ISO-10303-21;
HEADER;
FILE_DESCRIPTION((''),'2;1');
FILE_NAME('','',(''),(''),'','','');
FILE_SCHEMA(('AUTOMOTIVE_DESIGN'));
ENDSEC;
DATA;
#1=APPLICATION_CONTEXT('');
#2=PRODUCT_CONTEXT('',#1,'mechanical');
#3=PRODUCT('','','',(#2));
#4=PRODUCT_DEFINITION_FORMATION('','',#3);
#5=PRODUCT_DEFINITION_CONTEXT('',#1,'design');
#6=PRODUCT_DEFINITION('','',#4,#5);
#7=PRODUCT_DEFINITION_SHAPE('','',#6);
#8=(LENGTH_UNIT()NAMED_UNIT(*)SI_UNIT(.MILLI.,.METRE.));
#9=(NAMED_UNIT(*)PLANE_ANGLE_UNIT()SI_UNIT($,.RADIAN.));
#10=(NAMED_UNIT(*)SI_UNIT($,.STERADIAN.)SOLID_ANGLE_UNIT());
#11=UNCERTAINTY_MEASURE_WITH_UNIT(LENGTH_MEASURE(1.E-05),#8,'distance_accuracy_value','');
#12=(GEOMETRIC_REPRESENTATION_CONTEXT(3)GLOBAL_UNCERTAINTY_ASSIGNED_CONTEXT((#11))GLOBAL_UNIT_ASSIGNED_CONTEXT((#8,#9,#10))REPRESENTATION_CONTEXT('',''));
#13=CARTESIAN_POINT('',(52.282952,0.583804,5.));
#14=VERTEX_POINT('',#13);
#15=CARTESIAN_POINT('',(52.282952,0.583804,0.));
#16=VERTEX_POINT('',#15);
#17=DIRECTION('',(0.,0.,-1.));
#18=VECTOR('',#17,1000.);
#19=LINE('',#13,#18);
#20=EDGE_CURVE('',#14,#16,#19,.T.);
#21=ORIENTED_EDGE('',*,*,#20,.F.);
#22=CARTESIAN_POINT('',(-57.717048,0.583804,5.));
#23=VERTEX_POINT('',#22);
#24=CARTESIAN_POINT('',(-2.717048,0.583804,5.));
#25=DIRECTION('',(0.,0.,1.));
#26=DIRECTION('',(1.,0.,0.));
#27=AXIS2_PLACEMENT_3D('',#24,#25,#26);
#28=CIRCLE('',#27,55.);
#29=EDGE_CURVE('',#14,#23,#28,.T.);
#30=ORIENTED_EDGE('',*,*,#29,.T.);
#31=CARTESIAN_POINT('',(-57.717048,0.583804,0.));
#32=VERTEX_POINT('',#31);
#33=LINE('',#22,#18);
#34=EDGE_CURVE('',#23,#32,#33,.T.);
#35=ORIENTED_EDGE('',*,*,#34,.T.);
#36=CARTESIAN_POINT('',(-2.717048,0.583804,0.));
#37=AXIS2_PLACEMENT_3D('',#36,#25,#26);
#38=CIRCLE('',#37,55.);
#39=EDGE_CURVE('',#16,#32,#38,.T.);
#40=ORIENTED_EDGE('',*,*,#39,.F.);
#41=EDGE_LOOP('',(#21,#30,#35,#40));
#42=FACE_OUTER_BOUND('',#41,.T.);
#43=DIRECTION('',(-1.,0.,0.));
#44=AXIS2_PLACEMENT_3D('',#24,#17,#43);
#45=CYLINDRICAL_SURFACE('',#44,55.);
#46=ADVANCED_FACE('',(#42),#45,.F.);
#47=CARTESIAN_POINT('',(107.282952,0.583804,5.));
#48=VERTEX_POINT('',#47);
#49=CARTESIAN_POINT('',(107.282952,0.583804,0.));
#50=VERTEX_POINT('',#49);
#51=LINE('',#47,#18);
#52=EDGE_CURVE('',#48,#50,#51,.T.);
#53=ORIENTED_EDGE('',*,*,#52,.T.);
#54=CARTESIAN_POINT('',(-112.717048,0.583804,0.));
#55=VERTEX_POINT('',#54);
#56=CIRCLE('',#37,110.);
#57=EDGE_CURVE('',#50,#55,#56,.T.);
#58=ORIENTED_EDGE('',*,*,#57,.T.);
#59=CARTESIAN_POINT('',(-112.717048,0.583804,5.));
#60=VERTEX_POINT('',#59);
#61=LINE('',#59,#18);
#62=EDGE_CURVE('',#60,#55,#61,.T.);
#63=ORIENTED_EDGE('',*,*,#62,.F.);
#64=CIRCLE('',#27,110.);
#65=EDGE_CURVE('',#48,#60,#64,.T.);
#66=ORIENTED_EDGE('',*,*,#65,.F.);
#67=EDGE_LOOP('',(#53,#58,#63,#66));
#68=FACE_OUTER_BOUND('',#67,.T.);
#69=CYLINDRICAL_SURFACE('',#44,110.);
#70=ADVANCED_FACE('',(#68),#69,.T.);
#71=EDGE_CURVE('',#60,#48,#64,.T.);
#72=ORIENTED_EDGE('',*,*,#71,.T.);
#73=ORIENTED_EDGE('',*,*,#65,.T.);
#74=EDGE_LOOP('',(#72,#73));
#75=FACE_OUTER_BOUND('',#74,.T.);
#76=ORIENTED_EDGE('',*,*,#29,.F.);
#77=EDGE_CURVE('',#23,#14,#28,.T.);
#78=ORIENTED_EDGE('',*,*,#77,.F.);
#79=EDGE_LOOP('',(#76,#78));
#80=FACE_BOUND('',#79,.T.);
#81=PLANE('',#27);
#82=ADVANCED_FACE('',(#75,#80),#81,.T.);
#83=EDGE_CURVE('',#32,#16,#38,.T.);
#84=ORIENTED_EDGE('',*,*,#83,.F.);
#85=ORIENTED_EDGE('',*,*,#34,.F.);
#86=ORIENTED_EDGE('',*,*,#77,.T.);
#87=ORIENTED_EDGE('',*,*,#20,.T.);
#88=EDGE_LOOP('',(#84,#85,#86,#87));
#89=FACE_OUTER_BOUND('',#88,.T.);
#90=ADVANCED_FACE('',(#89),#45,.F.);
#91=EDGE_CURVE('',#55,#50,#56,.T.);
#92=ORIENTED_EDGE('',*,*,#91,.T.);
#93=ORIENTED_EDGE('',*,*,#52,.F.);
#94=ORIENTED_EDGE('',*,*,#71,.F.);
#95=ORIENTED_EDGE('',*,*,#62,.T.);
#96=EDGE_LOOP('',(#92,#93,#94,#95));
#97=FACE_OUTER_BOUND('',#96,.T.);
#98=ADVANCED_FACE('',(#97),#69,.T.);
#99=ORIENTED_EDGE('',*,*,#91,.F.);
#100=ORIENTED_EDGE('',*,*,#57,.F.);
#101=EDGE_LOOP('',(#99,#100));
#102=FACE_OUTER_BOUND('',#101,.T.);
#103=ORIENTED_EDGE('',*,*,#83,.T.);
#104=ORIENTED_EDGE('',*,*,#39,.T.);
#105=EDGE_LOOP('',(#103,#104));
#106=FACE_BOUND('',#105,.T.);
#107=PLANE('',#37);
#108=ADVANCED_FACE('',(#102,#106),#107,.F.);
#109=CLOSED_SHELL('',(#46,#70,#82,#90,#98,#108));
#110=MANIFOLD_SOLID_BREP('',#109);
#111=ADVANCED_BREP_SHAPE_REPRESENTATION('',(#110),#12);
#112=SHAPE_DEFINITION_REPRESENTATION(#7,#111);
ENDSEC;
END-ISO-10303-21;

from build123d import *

# Parameters (mm, degrees)
SKETCH1_R           = 110
SKETCH1_R_2         = 55
BOSS_EXTRUDE3_DEPTH = 5


with BuildPart() as part:
    # Sketch1 → Boss-Extrude3 (new body)
    with BuildSketch(Plane.XY):
        with Locations((-2.7170484, 0.583803612)):
            Circle(SKETCH1_R)
        with Locations((-2.7170484, 0.583803612)):
            Circle(SKETCH1_R_2, mode=Mode.SUBTRACT)
    extrude(amount=BOSS_EXTRUDE3_DEPTH)


solid = part.part
